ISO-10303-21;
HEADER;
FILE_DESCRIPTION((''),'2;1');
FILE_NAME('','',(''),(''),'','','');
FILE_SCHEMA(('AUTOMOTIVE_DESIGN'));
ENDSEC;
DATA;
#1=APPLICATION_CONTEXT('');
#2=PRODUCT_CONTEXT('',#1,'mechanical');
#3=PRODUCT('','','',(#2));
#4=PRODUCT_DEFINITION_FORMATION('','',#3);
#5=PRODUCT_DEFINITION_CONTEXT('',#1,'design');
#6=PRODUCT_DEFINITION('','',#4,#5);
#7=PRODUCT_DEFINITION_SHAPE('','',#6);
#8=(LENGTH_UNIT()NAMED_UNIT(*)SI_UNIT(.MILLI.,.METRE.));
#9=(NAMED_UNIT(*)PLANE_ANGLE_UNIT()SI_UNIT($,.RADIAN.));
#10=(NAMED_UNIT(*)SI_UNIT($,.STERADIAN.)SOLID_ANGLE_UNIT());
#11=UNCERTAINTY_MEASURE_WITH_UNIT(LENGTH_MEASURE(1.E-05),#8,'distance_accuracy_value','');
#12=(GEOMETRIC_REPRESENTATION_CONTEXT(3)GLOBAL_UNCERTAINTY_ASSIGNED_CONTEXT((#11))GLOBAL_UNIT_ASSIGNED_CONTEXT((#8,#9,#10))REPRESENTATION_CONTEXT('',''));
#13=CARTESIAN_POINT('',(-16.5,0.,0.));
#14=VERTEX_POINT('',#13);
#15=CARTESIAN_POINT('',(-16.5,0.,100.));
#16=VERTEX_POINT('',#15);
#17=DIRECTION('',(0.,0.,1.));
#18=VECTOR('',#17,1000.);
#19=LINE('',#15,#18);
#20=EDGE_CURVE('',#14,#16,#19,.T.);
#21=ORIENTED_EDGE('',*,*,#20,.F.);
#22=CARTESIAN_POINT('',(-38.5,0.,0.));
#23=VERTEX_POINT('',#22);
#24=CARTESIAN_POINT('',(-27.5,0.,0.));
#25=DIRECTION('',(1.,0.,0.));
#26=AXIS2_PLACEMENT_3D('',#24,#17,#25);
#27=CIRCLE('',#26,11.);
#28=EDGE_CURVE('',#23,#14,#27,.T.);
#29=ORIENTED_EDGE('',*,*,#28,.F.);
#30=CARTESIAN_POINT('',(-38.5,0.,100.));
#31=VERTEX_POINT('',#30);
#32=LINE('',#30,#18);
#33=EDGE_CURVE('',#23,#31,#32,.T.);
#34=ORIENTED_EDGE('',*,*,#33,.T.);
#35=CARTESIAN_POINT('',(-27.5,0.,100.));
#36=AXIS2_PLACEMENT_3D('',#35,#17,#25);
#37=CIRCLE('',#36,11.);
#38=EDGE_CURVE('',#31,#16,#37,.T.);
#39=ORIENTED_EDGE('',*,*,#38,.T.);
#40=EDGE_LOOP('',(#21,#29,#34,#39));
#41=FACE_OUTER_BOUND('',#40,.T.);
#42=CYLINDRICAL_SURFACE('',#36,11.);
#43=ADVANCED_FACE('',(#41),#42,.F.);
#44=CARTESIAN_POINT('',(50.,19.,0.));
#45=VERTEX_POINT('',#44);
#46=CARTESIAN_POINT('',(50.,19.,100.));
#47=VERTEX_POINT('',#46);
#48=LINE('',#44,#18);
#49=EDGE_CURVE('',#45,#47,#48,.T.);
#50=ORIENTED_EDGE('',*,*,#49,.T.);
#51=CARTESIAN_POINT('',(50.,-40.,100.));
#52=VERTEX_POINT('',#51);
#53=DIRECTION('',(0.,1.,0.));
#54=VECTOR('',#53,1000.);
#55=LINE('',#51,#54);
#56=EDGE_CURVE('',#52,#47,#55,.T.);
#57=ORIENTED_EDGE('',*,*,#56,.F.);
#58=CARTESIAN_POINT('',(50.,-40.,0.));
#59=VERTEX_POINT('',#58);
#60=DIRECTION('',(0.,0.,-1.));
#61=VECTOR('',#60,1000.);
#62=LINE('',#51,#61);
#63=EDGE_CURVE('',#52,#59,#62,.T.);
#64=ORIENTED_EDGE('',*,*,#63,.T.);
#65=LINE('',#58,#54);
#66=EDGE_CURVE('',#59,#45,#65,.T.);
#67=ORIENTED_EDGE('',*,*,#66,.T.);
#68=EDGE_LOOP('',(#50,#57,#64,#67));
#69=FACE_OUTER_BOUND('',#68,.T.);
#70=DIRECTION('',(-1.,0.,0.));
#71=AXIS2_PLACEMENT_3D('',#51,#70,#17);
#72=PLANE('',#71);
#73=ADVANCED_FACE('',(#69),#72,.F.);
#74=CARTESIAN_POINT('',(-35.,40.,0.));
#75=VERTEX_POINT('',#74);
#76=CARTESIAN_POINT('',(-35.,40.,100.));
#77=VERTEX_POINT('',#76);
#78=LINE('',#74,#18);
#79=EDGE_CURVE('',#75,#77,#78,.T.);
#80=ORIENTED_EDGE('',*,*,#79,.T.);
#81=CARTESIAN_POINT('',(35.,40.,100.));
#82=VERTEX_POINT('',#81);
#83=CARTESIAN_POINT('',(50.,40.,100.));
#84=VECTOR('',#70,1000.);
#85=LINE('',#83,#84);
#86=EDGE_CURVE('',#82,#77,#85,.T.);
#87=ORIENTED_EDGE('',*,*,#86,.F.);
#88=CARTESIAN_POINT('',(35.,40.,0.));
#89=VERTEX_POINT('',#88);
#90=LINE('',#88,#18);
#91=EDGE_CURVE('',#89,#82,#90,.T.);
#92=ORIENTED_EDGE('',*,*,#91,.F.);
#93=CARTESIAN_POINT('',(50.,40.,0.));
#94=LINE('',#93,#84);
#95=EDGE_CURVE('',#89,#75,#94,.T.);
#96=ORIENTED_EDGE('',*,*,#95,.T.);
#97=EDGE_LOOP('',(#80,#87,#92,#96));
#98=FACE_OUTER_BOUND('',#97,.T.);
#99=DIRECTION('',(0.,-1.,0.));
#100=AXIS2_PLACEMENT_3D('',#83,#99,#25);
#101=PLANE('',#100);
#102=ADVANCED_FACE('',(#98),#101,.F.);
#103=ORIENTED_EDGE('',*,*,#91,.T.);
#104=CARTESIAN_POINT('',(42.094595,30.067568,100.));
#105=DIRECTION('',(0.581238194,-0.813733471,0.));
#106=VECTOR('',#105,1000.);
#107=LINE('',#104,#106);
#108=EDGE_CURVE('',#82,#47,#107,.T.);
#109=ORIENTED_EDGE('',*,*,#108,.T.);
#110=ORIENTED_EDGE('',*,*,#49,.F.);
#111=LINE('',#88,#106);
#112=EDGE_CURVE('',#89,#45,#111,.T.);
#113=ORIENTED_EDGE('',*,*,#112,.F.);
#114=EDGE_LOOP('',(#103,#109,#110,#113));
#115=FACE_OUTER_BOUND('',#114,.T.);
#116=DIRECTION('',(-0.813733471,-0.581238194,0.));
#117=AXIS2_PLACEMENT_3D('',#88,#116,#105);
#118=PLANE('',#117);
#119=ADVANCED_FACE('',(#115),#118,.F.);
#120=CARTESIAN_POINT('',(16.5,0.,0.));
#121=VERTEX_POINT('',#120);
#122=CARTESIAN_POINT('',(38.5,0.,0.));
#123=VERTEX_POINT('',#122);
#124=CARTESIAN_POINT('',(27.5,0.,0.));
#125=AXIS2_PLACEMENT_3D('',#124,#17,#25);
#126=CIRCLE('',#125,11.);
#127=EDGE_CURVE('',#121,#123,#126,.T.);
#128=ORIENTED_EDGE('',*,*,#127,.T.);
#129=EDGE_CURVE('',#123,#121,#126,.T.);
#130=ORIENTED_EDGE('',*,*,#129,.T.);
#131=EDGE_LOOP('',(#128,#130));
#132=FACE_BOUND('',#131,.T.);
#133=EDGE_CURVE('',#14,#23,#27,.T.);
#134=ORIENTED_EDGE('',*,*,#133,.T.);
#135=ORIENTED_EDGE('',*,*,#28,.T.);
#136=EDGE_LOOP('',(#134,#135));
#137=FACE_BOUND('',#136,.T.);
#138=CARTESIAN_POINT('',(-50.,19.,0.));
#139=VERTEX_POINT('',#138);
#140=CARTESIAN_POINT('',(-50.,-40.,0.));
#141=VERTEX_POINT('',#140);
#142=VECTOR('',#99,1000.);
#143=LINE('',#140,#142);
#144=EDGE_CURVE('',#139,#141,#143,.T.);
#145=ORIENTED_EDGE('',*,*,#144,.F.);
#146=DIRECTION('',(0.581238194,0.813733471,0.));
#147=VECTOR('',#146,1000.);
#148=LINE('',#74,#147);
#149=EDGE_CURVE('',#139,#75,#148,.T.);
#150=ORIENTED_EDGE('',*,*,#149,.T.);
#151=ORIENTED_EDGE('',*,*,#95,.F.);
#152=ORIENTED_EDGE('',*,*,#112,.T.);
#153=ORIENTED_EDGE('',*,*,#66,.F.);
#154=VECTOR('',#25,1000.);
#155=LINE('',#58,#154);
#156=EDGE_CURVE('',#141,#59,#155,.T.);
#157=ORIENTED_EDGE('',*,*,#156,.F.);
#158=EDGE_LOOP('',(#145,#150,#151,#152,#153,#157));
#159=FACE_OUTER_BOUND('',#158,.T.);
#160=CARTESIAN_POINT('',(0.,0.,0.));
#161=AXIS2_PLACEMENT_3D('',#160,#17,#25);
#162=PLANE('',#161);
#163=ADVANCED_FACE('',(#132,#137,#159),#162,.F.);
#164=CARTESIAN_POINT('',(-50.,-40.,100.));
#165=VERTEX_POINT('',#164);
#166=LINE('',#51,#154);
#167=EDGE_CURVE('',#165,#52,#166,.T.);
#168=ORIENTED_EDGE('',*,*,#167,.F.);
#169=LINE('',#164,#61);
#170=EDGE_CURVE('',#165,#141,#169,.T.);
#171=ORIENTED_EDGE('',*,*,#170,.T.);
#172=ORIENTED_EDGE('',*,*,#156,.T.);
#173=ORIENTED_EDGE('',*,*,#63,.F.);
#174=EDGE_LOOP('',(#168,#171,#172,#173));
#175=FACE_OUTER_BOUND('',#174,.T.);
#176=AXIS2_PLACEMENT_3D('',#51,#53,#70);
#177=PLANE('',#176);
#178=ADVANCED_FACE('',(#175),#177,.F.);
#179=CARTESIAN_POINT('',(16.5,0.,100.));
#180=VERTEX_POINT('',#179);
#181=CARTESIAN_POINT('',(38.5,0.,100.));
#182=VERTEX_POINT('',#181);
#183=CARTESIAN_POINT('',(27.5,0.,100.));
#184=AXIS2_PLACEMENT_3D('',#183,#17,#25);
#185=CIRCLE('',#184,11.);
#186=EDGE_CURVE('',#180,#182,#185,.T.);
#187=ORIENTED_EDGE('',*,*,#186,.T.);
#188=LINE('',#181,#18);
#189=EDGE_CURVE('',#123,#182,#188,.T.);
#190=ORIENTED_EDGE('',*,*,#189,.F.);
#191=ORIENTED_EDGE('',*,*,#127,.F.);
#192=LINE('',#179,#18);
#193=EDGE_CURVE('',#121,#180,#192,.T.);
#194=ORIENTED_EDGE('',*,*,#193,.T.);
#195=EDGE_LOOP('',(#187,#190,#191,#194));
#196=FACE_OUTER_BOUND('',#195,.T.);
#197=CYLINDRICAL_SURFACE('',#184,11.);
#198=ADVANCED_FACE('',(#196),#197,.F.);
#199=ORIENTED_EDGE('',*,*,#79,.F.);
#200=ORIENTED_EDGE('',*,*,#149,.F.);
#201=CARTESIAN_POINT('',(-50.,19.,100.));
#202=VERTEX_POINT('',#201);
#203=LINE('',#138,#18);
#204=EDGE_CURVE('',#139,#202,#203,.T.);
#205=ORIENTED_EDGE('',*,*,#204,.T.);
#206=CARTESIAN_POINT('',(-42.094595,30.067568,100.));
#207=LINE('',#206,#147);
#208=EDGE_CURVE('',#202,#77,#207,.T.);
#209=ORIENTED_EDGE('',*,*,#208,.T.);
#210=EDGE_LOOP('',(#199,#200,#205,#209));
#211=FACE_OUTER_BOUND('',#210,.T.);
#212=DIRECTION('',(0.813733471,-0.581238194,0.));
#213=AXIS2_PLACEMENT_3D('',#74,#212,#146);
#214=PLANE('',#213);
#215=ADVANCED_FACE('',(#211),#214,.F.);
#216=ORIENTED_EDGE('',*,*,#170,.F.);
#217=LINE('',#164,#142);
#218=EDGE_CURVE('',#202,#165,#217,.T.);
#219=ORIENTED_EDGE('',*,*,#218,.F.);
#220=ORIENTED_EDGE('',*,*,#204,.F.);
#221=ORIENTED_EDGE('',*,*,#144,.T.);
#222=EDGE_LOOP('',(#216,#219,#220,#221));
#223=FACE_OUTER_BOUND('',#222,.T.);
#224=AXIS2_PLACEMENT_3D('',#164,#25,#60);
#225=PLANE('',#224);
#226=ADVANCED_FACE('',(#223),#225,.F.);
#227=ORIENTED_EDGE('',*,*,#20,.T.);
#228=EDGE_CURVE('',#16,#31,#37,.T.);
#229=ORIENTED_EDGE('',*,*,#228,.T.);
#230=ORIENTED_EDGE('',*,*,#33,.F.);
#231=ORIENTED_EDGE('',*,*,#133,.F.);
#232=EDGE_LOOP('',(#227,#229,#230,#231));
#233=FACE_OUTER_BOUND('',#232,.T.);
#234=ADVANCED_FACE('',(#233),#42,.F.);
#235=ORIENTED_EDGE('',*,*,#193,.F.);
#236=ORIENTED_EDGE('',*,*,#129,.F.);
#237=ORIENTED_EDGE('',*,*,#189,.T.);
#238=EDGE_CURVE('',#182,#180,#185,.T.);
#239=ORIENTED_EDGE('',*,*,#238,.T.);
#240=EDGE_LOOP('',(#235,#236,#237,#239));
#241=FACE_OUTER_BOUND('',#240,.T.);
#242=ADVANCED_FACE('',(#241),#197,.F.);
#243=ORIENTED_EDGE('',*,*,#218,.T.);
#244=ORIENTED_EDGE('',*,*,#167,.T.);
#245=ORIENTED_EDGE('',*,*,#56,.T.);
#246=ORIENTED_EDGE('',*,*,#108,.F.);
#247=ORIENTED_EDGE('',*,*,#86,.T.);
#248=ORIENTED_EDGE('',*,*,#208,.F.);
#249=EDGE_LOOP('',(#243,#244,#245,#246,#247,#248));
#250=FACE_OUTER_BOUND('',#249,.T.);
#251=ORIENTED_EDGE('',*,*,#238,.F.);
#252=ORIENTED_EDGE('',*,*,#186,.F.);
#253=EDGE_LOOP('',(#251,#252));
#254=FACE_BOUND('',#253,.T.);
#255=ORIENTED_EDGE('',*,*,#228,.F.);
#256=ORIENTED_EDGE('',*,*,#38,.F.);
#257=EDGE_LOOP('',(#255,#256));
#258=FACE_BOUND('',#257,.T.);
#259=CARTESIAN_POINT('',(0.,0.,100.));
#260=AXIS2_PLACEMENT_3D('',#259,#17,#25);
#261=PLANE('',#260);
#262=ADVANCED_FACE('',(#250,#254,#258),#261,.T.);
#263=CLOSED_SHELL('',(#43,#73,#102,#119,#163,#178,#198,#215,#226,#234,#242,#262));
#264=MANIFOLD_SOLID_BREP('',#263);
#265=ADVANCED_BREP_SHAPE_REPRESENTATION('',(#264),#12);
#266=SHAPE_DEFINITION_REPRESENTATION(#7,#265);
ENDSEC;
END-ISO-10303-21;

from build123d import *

# Parameters (mm, degrees)
SKETCH1_W               = 100
SKETCH1_H               = 80
BOSS_EXTRUDE1_DEPTH     = 100
CHAMFER1_SIZE           = 10
F_22_DIAMETER_HOLE1_D   = 22
CUT_EXTRUDE1_DEPTH      = 119.74342087
CUT_EXTRUDE1_DEPTH_BACK = 119.74342087


with BuildPart() as part:
    # Sketch1 → Boss-Extrude1 (new body)
    with BuildSketch(Plane.XY):
        Rectangle(SKETCH1_W, SKETCH1_H)
    extrude(amount=BOSS_EXTRUDE1_DEPTH)

    # Chamfer1
    chamfer1_edges = [part.edges().sort_by_distance(p)[0] for p in [
        (-50, 40, 50),
        (50, 40, 50),
    ]]
    chamfer(chamfer1_edges, length=CHAMFER1_SIZE)

    # Ø22 diameter hole1 (through all)
    with Locations(Plane.XY.offset(100)):
        with Locations((-27.5, 0), (27.5, 0)):
            Hole(F_22_DIAMETER_HOLE1_D / 2)

    # Sketch4 → Cut-Extrude1 (cut, two sides: drawn at the far end of the back side and taken through both)
    with BuildSketch(Plane.XY.offset(100).offset(-CUT_EXTRUDE1_DEPTH_BACK)):
        Polygon((-35, 40), (-50, 19), (-50, 40), align=None)
        Polygon((50, 40), (35, 40), (50, 19), align=None)
    extrude(amount=CUT_EXTRUDE1_DEPTH + CUT_EXTRUDE1_DEPTH_BACK, mode=Mode.SUBTRACT)


solid = part.part
